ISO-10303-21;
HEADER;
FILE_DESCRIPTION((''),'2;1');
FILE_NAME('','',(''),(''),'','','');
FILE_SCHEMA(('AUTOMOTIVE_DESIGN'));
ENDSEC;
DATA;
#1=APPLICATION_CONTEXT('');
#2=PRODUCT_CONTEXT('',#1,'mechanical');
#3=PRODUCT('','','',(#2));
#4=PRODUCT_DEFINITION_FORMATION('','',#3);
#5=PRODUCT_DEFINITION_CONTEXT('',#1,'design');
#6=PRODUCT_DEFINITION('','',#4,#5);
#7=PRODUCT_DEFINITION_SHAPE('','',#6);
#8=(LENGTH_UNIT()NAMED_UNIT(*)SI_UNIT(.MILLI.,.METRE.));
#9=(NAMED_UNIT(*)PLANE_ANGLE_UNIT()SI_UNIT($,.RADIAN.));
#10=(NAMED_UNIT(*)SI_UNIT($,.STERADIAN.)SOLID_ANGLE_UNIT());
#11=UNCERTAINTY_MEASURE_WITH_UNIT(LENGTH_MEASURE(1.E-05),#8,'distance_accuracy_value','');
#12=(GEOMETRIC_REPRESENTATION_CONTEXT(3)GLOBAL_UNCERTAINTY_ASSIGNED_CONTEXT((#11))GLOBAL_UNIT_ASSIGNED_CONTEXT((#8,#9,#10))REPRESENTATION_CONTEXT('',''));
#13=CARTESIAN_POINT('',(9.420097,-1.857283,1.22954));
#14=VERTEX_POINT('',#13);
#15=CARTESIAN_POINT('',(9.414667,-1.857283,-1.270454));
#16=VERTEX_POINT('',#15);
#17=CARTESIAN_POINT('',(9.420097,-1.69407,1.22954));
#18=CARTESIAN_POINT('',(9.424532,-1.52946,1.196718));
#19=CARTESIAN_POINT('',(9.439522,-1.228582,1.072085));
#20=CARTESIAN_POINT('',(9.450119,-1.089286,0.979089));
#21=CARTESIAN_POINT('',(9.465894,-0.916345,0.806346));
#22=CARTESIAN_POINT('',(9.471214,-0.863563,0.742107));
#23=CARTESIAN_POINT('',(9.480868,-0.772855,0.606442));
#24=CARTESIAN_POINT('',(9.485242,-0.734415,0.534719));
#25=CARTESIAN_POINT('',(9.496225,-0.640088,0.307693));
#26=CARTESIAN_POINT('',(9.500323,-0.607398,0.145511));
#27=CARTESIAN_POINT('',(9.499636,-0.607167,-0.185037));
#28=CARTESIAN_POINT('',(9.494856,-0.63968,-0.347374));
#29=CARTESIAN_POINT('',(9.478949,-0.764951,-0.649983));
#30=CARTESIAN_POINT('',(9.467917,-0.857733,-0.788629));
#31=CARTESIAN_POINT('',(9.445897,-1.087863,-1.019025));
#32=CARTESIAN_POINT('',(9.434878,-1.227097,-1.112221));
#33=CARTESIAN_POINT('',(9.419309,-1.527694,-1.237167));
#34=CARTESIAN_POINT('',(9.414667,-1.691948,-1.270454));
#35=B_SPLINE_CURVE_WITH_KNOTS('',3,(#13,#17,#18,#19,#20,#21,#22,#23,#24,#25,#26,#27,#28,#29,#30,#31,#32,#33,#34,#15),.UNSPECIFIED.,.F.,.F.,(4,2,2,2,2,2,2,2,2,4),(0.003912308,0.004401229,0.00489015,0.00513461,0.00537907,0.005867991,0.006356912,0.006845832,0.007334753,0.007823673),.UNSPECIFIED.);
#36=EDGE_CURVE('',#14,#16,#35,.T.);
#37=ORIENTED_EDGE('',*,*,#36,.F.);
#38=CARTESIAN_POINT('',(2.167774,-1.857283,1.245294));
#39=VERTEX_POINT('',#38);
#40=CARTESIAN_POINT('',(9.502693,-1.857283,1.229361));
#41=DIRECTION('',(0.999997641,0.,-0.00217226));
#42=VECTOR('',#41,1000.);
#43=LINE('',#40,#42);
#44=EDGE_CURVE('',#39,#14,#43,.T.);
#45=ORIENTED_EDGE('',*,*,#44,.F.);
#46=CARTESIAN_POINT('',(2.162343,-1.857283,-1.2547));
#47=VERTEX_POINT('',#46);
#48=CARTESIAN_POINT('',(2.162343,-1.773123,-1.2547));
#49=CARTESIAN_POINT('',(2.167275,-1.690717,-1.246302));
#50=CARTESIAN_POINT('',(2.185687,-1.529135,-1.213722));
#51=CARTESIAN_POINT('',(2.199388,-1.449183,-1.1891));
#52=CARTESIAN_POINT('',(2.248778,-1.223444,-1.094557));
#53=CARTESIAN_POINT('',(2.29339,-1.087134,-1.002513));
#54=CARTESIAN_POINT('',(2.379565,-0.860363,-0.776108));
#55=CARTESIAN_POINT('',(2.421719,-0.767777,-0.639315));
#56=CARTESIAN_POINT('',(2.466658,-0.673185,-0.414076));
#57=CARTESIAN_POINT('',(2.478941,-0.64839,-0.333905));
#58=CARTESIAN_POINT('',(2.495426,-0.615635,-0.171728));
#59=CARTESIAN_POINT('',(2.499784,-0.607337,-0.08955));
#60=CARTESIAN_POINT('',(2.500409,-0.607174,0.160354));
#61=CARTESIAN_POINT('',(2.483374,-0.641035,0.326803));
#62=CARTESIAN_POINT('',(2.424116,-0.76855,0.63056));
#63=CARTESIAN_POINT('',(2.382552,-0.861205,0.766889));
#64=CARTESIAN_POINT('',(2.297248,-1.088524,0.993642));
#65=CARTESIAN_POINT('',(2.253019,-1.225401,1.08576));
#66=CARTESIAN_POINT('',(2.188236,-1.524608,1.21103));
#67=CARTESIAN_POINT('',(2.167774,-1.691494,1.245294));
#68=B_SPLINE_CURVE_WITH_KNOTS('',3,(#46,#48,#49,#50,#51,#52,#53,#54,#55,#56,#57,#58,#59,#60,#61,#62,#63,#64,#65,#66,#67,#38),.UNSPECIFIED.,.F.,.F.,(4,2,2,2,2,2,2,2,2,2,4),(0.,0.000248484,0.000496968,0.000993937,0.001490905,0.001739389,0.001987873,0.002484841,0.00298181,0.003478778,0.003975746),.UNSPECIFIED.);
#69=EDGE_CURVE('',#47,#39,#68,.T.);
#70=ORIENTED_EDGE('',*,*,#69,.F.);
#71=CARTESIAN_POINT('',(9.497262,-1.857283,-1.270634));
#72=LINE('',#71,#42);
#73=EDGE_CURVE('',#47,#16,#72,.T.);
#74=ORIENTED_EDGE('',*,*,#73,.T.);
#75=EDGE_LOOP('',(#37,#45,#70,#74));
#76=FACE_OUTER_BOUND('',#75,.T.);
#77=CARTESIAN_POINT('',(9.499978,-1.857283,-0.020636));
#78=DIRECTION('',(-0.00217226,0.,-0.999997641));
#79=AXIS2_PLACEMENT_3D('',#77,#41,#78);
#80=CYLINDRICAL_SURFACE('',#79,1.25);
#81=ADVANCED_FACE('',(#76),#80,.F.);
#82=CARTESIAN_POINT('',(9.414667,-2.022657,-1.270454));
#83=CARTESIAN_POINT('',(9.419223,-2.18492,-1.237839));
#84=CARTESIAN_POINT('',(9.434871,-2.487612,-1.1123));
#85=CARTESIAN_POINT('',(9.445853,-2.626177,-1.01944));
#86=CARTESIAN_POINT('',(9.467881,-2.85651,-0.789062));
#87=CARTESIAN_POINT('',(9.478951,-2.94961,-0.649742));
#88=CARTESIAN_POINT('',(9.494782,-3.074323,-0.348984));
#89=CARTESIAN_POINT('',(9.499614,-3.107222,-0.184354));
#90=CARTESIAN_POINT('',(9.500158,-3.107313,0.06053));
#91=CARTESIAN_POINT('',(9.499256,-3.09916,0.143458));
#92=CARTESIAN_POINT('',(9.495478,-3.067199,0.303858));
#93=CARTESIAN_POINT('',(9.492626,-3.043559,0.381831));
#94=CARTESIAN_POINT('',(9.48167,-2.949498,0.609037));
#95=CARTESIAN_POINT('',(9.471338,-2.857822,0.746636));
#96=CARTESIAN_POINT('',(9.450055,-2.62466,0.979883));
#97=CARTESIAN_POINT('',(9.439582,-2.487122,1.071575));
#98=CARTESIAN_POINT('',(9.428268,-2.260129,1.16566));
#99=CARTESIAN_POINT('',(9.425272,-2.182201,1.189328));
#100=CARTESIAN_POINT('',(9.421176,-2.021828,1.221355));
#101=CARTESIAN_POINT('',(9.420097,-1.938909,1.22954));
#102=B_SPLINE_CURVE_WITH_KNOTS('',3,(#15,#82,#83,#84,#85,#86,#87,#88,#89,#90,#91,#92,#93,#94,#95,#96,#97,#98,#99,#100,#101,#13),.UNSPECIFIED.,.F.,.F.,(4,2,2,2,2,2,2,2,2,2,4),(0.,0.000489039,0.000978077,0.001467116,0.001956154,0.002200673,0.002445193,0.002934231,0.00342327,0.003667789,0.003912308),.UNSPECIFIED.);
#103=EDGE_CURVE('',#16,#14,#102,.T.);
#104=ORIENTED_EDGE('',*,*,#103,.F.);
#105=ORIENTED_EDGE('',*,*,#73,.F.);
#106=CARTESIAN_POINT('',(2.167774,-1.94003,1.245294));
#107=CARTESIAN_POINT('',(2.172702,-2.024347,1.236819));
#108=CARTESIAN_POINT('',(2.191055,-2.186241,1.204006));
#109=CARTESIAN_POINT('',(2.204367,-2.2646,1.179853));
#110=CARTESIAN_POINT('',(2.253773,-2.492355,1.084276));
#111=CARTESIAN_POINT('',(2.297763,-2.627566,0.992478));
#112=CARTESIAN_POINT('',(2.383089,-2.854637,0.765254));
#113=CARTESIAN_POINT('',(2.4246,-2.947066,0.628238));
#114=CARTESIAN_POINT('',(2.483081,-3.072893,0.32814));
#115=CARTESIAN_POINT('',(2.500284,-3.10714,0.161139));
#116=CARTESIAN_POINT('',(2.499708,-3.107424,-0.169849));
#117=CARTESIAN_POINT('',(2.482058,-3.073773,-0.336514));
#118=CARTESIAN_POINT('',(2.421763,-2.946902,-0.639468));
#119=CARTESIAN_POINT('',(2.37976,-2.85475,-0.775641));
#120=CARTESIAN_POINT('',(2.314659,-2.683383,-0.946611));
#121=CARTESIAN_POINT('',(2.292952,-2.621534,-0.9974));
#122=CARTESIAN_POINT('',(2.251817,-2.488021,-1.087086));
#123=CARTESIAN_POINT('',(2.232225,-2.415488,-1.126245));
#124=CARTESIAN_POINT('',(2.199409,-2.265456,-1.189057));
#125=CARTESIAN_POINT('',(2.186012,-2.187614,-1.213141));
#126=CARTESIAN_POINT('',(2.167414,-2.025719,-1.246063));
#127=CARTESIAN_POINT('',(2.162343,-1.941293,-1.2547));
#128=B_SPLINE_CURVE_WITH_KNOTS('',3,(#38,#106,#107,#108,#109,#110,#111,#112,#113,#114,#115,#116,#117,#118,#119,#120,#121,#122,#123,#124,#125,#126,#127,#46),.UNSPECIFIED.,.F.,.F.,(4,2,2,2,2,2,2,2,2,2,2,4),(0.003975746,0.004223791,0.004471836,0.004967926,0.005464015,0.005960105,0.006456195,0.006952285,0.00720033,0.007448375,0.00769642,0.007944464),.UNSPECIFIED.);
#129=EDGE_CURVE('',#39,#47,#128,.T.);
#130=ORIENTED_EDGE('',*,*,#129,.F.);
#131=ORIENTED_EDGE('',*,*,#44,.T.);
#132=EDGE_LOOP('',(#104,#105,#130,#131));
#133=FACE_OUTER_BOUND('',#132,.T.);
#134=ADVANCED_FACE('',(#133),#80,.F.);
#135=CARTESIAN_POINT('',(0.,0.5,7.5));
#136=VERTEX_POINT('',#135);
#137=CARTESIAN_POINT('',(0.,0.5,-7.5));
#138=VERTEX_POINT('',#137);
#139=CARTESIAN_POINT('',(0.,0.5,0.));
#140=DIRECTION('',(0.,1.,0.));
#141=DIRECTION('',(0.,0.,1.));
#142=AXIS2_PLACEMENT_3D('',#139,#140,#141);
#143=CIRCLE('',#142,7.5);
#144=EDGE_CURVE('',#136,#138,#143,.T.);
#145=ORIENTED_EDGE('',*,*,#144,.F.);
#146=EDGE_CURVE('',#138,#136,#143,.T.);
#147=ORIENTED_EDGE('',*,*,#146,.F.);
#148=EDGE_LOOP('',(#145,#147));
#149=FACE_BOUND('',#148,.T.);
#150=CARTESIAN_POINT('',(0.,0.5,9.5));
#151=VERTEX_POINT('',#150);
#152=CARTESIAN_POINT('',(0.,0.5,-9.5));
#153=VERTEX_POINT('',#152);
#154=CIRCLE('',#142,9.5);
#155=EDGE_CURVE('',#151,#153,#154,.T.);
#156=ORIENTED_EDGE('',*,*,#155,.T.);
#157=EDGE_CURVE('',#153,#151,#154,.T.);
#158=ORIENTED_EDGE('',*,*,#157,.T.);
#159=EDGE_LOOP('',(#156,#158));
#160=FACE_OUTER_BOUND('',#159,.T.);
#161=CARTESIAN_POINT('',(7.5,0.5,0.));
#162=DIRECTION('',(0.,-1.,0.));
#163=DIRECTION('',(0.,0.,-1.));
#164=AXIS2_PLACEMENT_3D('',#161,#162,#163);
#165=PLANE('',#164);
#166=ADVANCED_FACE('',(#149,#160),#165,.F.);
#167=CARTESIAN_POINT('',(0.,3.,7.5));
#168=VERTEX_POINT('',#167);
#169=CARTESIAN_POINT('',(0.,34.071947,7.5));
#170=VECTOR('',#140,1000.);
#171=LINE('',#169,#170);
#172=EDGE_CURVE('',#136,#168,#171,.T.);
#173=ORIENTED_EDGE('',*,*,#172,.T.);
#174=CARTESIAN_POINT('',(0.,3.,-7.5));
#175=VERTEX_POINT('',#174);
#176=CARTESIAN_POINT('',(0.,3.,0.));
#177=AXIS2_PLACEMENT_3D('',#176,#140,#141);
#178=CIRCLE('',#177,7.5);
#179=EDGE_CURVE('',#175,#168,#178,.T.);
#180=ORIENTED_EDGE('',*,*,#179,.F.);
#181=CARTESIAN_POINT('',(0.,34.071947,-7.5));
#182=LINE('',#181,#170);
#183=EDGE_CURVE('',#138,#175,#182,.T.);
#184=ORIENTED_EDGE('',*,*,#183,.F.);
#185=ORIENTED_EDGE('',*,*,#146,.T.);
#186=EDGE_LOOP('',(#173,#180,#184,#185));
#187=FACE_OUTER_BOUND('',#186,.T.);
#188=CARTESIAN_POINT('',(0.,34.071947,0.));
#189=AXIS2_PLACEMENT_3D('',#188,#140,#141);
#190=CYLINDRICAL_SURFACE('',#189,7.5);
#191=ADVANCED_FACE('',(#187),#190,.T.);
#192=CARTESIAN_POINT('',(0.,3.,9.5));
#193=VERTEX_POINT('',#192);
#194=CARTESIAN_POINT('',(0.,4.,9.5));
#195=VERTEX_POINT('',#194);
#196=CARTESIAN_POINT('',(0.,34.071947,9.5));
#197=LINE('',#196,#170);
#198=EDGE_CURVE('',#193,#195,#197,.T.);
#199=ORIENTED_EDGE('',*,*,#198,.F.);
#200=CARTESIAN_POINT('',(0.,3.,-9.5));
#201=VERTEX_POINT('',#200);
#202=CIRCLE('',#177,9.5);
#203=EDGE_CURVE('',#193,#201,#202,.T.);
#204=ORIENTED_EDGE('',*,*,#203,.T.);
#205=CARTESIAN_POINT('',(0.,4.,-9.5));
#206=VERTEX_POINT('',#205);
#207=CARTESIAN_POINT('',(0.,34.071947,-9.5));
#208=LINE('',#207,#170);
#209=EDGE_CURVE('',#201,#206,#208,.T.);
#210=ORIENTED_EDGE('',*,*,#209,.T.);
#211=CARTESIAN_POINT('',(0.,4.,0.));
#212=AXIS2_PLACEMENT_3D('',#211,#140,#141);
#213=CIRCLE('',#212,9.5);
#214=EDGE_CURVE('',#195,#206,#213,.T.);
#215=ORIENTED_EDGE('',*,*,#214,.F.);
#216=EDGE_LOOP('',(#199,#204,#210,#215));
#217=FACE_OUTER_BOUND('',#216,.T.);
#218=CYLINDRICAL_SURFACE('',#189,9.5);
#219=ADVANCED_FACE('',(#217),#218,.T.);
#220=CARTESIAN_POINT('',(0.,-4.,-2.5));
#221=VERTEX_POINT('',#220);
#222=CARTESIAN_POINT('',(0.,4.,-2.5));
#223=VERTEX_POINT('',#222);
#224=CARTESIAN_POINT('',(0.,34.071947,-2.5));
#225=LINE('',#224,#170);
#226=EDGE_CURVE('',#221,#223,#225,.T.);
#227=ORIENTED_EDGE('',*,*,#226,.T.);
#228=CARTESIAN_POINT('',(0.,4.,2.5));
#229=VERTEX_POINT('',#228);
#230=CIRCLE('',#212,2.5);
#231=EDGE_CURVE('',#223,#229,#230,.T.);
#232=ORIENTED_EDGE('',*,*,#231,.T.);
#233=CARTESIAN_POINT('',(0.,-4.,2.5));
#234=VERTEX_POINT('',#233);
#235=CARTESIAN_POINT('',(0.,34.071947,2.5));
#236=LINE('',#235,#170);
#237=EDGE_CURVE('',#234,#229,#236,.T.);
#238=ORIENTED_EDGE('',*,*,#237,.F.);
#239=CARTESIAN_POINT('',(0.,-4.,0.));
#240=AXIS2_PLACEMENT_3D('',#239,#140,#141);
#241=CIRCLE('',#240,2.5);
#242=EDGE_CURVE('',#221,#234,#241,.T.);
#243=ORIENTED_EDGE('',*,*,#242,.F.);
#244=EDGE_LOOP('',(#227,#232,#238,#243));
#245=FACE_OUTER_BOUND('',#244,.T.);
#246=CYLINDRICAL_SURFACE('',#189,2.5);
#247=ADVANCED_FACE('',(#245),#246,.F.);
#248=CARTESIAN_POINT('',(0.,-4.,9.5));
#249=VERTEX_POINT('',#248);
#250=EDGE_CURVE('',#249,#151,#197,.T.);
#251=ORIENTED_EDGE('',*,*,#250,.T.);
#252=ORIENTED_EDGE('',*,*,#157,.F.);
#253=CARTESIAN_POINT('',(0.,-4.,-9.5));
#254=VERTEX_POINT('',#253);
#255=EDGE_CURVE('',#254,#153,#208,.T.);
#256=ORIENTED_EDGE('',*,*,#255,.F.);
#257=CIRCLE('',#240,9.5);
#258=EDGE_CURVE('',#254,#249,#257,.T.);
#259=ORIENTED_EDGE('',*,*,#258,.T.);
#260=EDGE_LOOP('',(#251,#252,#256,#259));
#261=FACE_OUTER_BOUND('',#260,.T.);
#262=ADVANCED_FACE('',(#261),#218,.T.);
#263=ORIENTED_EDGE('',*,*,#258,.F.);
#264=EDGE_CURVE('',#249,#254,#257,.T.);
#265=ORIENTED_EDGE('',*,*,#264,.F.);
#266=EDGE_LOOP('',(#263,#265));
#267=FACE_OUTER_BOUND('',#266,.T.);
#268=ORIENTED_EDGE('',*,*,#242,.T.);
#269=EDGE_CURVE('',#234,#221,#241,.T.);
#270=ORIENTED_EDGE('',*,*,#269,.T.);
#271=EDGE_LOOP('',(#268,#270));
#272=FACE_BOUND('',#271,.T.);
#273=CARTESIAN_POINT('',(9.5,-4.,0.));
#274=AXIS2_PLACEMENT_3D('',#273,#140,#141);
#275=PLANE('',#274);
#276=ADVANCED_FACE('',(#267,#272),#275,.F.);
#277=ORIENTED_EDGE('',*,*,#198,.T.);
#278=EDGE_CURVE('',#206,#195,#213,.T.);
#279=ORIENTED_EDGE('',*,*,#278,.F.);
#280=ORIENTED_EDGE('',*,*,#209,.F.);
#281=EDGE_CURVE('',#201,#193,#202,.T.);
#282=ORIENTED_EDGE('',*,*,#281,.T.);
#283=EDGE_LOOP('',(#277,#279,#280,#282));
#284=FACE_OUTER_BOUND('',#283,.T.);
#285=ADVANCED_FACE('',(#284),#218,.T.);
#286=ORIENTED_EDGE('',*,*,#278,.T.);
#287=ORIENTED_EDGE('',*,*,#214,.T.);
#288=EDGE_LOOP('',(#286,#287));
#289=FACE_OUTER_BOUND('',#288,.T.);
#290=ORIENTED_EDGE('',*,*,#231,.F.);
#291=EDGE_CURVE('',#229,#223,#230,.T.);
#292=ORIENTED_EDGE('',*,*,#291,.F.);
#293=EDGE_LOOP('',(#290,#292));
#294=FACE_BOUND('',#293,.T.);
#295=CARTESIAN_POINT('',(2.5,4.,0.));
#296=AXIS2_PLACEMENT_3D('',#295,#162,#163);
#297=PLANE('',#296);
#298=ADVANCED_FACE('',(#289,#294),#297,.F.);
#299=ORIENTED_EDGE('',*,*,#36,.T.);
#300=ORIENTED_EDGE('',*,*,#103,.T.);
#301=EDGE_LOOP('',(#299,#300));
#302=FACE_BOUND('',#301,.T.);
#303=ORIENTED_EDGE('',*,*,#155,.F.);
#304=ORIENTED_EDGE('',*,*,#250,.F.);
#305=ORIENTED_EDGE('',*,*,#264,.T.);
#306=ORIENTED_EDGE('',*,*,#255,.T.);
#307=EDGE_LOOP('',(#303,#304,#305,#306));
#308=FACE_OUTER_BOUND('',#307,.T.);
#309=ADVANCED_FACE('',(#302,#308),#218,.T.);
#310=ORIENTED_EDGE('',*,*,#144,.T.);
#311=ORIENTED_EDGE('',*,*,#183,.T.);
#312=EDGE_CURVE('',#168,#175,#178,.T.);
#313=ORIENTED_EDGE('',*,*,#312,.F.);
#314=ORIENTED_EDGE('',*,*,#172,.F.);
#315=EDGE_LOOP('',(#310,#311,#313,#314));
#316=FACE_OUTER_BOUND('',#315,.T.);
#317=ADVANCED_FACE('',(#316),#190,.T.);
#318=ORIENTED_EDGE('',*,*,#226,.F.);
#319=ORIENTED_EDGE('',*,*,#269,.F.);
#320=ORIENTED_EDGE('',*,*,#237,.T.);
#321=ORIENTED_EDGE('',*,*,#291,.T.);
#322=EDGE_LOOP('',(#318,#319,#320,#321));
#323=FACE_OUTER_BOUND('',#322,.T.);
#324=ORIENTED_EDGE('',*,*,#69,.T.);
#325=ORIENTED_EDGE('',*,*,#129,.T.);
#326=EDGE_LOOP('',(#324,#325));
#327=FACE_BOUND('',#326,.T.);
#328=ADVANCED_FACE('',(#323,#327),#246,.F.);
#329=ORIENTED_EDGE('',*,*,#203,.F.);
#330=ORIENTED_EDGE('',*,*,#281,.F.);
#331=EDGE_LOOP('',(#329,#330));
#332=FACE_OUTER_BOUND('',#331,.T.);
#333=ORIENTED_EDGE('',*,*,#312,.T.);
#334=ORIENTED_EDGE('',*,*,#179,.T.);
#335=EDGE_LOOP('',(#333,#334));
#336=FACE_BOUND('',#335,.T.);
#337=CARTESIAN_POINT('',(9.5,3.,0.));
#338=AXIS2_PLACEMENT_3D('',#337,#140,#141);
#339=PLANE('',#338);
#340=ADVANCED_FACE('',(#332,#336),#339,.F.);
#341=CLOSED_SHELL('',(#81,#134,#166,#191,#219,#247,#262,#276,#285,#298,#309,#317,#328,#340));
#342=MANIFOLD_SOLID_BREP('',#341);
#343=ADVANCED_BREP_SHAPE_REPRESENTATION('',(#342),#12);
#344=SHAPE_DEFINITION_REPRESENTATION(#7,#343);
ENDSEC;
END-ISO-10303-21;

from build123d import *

# Parameters (mm, degrees)
HOLE_WIZARD_M3_1_REACH  = 24.044
HOLE_WIZARD_M3_1_BORE_R = 1.25


with BuildPart() as part:
    # 草图1 → 旋转1 (revolve)
    with BuildSketch(Plane.XY, mode=Mode.PRIVATE) as revolve_1_sk:
        Polygon((2.5, 4), (2.5, -4), (9.5, -4), (9.5, 0.5), (7.5, 0.5), (7.5, 3), (9.5, 3), (9.5, 4), align=None)
    revolve(revolve_1_sk.sketch.rotate(Axis((0, 34.071946617, 0), (0, -1, 0)), 90), axis=Axis((0, 34.071946617, 0), (0, -1, 0)))

    # M3 螺纹孔1 bore (on position points) → M3 螺纹孔1 (cut, up to next)
    with BuildSketch(Plane(origin=(9.499977586, -1.857282502, -0.020636472), x_dir=(0.002172260237, 0, 0.99999764064), z_dir=(0.99999764064, 0, -0.002172260237)), mode=Mode.PRIVATE) as hole_wizard_m3_1_sk1:
        Circle(HOLE_WIZARD_M3_1_BORE_R)
    hole_wizard_m3_1_tool1 = extrude(hole_wizard_m3_1_sk1.sketch, amount=-HOLE_WIZARD_M3_1_REACH, mode=Mode.PRIVATE) & part.part
    add(hole_wizard_m3_1_tool1.solids().sort_by_distance((9.499978, -1.857283, -0.020636))[0], mode=Mode.SUBTRACT)


solid = part.part
